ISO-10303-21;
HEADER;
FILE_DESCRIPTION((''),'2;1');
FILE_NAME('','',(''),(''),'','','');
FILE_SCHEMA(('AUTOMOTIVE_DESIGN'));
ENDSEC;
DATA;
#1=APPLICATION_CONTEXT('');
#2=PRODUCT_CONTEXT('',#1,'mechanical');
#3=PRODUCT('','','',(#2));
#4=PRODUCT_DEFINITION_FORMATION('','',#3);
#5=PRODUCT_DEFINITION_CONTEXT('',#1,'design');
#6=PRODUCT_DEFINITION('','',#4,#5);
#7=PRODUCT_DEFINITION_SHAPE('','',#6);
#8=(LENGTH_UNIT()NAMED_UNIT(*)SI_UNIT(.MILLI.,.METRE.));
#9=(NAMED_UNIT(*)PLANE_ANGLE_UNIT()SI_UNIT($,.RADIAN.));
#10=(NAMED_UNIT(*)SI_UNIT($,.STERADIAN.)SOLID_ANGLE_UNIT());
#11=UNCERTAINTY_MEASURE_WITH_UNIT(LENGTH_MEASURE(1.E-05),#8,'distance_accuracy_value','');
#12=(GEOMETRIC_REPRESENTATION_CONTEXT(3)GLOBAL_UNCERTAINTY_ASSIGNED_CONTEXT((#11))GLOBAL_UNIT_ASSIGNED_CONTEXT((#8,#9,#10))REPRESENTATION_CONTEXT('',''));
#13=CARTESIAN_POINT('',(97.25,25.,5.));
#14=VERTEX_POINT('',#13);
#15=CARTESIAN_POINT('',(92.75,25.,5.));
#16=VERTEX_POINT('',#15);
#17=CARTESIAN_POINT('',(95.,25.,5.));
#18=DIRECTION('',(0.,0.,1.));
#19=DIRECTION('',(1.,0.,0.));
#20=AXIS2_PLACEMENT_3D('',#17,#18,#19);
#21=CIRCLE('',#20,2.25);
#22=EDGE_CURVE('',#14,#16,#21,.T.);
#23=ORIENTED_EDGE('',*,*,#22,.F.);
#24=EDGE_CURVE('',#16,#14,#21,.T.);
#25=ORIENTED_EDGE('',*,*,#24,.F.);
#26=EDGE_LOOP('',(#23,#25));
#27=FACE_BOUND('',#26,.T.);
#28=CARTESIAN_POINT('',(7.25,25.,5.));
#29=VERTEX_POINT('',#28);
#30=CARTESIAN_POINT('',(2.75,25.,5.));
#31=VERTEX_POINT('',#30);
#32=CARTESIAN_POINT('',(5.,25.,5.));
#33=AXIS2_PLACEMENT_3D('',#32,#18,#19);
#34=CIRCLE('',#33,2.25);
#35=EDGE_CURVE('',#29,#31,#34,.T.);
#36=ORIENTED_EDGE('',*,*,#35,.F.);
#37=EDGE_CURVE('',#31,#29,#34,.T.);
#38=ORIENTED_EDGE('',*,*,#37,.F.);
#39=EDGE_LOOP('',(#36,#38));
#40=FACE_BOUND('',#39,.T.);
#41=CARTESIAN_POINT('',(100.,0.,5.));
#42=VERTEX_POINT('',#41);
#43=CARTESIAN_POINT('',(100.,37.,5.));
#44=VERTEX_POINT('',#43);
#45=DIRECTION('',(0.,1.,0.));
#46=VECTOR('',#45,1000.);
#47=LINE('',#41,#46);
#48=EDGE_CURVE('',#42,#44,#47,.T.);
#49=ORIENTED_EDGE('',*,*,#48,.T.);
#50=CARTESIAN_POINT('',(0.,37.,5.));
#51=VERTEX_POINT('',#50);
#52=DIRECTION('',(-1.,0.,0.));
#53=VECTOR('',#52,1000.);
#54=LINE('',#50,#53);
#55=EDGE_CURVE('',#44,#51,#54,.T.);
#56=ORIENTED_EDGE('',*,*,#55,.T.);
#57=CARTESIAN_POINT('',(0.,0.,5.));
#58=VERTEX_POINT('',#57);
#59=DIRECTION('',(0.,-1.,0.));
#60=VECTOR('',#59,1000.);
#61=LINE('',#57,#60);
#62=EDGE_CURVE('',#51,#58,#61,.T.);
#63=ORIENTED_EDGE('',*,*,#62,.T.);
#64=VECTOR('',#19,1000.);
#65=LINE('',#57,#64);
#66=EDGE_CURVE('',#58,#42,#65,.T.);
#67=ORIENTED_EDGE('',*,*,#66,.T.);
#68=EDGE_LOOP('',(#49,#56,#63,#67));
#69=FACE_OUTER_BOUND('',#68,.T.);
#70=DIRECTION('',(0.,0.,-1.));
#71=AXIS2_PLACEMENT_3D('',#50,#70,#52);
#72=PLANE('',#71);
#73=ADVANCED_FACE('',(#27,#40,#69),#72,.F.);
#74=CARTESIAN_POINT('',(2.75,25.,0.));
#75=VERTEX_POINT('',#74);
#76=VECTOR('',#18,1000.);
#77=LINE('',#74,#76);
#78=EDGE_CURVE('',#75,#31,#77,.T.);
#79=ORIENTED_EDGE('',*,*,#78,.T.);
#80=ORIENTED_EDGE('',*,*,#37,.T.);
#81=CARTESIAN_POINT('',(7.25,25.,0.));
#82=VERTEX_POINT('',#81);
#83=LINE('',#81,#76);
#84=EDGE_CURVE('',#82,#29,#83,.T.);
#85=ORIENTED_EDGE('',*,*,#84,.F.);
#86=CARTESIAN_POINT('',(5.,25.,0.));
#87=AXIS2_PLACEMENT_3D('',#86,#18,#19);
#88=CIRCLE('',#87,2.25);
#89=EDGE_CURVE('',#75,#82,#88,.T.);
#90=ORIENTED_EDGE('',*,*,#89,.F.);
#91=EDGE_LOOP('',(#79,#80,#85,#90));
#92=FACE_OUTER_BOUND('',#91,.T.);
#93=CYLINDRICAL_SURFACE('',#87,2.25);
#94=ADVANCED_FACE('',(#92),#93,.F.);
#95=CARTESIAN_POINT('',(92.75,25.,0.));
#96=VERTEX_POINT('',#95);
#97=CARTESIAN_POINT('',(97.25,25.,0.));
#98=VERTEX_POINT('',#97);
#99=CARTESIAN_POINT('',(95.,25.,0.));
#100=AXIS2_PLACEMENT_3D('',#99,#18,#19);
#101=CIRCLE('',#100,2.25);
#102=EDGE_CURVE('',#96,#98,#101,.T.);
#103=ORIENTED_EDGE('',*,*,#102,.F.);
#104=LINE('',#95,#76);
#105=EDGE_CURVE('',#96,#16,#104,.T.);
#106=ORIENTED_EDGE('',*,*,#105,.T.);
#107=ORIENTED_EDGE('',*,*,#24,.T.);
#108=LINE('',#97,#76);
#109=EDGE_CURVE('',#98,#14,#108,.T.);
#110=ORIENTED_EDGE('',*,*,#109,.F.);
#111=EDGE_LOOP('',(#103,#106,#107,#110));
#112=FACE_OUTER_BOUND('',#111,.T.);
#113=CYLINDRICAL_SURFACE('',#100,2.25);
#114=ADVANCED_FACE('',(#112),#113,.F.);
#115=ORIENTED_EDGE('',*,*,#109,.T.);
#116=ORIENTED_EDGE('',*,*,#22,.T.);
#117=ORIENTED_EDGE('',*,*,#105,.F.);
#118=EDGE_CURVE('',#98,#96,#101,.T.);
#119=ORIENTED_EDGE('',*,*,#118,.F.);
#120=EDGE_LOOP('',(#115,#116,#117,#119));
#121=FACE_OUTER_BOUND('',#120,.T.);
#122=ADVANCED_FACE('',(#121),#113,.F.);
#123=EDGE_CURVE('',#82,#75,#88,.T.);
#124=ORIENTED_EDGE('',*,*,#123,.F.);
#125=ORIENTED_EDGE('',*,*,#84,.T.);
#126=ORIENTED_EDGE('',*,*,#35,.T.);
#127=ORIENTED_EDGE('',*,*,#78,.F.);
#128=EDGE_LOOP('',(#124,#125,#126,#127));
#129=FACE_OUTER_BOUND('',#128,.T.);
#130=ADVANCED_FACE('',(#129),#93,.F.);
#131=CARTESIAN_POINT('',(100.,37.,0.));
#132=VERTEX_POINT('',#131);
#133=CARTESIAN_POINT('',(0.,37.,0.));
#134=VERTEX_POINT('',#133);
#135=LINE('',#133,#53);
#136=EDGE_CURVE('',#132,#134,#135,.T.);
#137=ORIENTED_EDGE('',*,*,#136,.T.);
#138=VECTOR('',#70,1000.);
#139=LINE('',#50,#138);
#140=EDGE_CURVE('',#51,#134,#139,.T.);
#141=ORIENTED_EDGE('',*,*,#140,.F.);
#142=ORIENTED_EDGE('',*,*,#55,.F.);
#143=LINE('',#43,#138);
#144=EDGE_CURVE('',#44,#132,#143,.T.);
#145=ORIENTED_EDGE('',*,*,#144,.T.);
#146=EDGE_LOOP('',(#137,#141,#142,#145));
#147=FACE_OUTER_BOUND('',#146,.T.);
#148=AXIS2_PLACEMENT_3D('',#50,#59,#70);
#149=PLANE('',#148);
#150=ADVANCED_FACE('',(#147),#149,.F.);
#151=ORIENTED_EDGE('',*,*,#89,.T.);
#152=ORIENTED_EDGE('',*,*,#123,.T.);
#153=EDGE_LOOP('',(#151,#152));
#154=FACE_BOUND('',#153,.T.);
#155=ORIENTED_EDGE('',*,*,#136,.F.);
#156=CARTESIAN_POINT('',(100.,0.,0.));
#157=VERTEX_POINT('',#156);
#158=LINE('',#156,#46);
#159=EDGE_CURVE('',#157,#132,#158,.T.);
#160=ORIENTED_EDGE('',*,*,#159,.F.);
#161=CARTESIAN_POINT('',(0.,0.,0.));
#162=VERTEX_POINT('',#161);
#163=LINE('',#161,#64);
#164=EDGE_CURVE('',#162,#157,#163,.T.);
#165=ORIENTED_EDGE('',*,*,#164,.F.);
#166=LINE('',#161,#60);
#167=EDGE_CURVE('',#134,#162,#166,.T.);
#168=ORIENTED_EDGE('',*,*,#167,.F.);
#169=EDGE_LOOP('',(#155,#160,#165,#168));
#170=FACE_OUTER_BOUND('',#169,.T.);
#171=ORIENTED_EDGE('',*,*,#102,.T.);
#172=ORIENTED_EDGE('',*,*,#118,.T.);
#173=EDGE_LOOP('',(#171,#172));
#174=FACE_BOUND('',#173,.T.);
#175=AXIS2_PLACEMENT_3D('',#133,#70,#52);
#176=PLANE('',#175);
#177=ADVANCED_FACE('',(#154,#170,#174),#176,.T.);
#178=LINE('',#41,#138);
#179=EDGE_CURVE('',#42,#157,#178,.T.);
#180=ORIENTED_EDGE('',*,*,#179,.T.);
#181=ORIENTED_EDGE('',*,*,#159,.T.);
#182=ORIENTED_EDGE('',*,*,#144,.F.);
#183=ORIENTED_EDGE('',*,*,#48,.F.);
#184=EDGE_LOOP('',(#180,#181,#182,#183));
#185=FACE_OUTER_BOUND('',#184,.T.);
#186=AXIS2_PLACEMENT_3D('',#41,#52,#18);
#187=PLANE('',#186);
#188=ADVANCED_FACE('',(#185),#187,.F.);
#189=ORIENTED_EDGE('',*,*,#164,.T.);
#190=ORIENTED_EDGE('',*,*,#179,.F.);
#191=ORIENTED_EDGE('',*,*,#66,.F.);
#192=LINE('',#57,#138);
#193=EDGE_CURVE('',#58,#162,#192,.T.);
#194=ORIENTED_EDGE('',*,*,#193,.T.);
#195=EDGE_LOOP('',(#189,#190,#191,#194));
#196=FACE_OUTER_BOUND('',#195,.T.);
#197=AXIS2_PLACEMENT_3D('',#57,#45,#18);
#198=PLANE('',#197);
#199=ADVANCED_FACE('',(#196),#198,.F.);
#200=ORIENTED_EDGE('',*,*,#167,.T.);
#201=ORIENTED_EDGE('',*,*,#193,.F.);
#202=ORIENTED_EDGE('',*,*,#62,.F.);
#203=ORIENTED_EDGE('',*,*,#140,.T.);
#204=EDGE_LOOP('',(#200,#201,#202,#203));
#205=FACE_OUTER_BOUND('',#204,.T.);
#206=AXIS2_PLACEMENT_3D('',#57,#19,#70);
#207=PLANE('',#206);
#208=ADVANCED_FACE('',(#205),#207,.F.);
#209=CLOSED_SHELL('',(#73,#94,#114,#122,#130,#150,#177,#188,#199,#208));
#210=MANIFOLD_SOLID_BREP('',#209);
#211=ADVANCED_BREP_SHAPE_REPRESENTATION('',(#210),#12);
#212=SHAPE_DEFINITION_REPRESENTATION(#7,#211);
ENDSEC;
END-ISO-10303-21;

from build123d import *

# Parameters (mm, degrees)
SKETCH_1_W          = 100
SKETCH_1_H          = 37
EXTRUDE_1_DEPTH     = 5
SKETCH_2_R          = 2.25
CUT_EXTRUDE_1_DEPTH = 5


with BuildPart() as part:
    # 草图1 → 凸台-拉伸1 (new body)
    with BuildSketch(Plane.XY):
        with Locations((50, 18.5)):
            Rectangle(SKETCH_1_W, SKETCH_1_H)
    extrude(amount=EXTRUDE_1_DEPTH)

    # 草图2 → 切除-拉伸1 (cut)
    with BuildSketch(Plane.XY.offset(5)):
        with Locations((5, 25)):
            Circle(SKETCH_2_R)
        with Locations((95, 25)):
            Circle(SKETCH_2_R)
    extrude(amount=-CUT_EXTRUDE_1_DEPTH, mode=Mode.SUBTRACT)


solid = part.part
